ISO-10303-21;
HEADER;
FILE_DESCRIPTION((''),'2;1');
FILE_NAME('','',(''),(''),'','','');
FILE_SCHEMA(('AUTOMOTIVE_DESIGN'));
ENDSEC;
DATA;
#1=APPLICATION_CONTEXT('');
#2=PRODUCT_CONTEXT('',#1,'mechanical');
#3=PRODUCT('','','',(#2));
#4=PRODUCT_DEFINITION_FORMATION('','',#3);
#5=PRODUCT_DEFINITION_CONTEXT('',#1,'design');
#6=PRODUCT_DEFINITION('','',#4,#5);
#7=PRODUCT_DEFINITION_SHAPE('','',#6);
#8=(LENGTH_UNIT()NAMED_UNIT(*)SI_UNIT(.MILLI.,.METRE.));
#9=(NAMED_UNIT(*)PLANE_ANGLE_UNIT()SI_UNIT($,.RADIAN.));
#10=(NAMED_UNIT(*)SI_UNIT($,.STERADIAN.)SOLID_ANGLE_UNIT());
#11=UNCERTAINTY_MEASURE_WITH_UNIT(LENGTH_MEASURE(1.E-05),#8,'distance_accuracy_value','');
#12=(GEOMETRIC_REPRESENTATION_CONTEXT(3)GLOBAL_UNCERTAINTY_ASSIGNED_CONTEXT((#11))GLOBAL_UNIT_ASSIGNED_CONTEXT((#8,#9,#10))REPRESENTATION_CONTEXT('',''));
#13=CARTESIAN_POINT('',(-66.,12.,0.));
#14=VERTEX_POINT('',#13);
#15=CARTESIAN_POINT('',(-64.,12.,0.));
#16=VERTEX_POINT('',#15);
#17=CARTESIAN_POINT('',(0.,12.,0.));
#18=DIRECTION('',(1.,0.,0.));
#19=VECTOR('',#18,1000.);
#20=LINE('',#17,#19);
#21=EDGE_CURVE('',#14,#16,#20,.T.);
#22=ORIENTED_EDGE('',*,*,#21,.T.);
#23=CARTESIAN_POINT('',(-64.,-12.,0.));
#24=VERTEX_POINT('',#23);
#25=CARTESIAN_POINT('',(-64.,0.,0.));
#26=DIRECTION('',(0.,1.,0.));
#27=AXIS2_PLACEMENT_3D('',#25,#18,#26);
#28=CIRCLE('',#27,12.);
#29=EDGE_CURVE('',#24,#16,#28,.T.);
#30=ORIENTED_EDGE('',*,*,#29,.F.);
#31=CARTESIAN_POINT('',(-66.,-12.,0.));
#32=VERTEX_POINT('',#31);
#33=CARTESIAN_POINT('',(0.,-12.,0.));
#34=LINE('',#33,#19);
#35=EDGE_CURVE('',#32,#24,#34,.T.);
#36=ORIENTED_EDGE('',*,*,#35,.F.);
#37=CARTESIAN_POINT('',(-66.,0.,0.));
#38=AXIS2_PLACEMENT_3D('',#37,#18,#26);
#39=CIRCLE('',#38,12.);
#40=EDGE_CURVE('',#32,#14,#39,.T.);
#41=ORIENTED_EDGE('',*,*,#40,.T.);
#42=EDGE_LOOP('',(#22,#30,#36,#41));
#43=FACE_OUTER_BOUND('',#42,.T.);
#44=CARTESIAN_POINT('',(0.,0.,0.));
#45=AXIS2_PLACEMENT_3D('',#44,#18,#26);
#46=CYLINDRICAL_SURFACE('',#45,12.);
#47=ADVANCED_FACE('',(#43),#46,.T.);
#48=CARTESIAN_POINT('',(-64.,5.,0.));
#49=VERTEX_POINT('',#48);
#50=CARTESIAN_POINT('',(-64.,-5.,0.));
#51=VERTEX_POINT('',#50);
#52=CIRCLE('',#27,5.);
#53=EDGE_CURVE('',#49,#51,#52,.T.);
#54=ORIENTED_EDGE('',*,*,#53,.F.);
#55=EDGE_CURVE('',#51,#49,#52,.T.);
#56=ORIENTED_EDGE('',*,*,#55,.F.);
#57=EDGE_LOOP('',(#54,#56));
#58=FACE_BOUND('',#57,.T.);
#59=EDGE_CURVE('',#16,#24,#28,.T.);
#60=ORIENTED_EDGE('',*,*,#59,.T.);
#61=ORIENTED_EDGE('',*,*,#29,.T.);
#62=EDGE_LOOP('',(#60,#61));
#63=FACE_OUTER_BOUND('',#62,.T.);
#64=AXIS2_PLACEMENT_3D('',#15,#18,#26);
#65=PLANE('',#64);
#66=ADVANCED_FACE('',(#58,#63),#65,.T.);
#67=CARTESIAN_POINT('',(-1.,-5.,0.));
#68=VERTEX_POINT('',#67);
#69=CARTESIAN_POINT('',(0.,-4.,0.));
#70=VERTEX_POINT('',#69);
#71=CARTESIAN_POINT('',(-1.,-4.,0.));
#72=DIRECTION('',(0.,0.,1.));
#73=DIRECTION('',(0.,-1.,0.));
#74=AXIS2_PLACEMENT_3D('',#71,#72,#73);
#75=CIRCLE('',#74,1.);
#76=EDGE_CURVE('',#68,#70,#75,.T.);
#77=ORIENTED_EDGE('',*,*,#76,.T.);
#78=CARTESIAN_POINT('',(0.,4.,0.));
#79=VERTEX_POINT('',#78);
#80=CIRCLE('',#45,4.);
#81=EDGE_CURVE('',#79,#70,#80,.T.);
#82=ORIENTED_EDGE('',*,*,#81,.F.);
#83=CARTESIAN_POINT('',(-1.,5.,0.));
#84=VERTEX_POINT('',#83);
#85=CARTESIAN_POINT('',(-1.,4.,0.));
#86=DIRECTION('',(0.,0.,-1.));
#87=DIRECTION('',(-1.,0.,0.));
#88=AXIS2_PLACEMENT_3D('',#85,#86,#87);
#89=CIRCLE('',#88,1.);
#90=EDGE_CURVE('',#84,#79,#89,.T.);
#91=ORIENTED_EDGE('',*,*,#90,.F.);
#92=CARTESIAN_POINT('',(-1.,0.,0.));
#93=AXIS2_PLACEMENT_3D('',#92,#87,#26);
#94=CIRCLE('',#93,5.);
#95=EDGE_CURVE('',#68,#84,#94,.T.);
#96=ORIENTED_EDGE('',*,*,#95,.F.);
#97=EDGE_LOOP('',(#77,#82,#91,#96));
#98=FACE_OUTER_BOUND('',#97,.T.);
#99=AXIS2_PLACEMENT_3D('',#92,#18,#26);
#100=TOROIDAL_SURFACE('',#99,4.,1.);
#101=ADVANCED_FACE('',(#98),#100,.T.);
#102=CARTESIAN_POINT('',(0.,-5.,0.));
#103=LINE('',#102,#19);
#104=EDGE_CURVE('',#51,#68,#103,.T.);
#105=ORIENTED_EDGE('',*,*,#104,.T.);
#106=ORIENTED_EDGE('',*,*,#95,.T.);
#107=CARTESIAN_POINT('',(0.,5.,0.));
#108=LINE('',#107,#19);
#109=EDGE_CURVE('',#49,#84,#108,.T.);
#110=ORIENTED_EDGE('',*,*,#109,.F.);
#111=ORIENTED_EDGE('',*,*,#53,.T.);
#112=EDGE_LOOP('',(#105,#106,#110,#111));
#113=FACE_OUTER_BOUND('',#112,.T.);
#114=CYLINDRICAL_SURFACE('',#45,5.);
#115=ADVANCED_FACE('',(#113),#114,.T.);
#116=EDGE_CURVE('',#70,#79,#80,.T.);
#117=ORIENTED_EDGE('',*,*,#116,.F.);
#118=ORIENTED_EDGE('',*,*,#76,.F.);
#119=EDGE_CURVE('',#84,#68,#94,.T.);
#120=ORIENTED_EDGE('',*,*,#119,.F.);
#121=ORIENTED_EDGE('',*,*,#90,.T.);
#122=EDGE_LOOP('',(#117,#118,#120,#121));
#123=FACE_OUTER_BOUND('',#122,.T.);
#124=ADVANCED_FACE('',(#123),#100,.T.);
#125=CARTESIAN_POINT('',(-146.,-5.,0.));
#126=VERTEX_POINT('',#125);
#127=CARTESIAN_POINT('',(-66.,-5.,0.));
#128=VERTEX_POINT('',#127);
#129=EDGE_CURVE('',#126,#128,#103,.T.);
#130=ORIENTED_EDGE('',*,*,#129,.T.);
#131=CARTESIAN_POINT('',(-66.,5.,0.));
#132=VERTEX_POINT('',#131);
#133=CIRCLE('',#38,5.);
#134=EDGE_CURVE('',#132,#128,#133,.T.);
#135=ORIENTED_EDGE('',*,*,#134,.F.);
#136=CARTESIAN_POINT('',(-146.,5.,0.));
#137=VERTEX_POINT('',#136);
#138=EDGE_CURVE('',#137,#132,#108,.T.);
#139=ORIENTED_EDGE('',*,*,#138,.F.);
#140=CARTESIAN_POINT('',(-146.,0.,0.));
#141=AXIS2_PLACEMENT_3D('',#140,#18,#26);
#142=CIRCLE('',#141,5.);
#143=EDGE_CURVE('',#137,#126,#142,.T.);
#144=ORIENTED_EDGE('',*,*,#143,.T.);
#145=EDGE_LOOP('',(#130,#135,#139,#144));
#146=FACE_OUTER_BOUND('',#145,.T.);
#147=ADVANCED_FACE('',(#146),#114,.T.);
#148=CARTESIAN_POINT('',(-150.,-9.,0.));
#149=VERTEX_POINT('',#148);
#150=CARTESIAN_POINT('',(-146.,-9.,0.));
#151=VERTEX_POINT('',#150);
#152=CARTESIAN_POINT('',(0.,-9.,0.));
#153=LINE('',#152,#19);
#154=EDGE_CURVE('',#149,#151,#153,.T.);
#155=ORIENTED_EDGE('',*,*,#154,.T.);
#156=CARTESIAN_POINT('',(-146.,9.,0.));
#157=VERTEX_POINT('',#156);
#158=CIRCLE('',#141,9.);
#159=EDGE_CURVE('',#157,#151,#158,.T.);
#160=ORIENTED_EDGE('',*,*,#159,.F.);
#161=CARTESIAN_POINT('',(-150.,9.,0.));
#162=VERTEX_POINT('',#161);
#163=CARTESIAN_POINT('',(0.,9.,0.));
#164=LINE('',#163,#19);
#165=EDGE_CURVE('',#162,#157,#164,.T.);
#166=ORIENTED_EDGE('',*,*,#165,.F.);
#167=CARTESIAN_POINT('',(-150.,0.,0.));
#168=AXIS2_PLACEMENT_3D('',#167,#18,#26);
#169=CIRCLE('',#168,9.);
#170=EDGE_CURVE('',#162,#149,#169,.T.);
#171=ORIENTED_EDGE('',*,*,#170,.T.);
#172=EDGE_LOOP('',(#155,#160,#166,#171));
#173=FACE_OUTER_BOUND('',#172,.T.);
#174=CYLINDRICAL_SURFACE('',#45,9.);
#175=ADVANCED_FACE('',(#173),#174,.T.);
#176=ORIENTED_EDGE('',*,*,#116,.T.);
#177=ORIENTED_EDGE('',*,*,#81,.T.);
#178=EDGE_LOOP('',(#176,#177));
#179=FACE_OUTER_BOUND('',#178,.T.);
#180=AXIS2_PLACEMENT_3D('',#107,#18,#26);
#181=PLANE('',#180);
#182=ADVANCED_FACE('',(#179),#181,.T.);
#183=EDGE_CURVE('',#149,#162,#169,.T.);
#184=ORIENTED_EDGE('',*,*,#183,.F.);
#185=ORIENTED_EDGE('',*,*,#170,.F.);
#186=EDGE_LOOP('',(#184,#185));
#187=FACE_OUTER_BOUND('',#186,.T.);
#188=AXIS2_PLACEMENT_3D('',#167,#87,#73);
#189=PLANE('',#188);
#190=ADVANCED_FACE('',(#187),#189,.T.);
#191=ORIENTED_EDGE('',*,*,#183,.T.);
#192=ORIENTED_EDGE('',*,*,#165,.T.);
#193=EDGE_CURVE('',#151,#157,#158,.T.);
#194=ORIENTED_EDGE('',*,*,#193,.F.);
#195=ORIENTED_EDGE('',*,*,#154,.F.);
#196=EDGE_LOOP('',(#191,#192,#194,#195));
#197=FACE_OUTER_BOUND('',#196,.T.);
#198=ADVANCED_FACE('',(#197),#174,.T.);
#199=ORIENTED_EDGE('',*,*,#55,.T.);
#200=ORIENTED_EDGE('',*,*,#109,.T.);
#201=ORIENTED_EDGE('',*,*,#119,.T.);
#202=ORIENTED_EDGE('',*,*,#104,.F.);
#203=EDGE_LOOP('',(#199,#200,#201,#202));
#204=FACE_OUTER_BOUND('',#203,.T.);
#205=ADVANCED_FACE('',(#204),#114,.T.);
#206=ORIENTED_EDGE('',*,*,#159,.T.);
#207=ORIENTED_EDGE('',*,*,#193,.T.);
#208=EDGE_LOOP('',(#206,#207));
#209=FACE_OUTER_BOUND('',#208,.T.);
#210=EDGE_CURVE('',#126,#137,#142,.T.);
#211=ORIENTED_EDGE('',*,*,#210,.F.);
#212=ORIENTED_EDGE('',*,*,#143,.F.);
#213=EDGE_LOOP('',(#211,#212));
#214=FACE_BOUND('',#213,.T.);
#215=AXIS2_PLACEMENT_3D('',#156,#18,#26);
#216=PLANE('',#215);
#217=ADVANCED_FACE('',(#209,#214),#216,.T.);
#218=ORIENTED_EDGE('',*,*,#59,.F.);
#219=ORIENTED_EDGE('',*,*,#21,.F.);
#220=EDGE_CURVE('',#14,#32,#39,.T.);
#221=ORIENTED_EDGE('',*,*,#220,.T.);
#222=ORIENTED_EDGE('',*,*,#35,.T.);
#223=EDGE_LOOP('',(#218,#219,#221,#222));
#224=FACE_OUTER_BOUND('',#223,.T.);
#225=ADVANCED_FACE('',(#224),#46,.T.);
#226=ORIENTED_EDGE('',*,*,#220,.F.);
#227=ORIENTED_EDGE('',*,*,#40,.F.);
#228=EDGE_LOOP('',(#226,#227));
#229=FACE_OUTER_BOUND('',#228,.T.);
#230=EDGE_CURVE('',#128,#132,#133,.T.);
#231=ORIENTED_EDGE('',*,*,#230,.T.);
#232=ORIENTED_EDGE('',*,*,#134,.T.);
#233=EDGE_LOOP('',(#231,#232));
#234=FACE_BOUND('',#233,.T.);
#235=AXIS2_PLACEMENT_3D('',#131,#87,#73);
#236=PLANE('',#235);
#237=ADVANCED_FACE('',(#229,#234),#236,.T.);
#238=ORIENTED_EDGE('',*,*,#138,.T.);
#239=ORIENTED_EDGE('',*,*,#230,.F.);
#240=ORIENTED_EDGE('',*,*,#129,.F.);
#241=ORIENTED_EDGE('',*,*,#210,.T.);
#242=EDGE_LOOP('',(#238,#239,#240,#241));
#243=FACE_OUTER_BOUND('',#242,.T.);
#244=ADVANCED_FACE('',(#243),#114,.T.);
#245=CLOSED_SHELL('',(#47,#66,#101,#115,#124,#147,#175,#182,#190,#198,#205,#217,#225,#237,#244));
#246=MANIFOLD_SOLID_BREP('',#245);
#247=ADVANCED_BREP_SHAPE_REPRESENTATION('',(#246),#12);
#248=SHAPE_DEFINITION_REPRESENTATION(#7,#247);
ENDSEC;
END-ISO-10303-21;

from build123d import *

# Parameters (mm, degrees)
EDGE_FILLET_R1_R = 1


with BuildPart() as part:
    # Shaft Profile Sketch → Shaft Body Revolve (revolve)
    with BuildSketch(Plane.XY):
        Polygon((-150, 0), (-150, 9), (-146, 9), (-146, 5), (-66, 5), (-66, 12), (-64, 12), (-64, 5), (0, 5), (0, 0), align=None)
    revolve(axis=Axis((0, 0, 0), (-1, 0, 0)))

    # Edge Fillet R1
    edge_fillet_r1_edges = [part.edges().sort_by_distance(p)[0] for p in [
        (0, -5, 0),
    ]]
    fillet(edge_fillet_r1_edges, radius=EDGE_FILLET_R1_R)


solid = part.part
